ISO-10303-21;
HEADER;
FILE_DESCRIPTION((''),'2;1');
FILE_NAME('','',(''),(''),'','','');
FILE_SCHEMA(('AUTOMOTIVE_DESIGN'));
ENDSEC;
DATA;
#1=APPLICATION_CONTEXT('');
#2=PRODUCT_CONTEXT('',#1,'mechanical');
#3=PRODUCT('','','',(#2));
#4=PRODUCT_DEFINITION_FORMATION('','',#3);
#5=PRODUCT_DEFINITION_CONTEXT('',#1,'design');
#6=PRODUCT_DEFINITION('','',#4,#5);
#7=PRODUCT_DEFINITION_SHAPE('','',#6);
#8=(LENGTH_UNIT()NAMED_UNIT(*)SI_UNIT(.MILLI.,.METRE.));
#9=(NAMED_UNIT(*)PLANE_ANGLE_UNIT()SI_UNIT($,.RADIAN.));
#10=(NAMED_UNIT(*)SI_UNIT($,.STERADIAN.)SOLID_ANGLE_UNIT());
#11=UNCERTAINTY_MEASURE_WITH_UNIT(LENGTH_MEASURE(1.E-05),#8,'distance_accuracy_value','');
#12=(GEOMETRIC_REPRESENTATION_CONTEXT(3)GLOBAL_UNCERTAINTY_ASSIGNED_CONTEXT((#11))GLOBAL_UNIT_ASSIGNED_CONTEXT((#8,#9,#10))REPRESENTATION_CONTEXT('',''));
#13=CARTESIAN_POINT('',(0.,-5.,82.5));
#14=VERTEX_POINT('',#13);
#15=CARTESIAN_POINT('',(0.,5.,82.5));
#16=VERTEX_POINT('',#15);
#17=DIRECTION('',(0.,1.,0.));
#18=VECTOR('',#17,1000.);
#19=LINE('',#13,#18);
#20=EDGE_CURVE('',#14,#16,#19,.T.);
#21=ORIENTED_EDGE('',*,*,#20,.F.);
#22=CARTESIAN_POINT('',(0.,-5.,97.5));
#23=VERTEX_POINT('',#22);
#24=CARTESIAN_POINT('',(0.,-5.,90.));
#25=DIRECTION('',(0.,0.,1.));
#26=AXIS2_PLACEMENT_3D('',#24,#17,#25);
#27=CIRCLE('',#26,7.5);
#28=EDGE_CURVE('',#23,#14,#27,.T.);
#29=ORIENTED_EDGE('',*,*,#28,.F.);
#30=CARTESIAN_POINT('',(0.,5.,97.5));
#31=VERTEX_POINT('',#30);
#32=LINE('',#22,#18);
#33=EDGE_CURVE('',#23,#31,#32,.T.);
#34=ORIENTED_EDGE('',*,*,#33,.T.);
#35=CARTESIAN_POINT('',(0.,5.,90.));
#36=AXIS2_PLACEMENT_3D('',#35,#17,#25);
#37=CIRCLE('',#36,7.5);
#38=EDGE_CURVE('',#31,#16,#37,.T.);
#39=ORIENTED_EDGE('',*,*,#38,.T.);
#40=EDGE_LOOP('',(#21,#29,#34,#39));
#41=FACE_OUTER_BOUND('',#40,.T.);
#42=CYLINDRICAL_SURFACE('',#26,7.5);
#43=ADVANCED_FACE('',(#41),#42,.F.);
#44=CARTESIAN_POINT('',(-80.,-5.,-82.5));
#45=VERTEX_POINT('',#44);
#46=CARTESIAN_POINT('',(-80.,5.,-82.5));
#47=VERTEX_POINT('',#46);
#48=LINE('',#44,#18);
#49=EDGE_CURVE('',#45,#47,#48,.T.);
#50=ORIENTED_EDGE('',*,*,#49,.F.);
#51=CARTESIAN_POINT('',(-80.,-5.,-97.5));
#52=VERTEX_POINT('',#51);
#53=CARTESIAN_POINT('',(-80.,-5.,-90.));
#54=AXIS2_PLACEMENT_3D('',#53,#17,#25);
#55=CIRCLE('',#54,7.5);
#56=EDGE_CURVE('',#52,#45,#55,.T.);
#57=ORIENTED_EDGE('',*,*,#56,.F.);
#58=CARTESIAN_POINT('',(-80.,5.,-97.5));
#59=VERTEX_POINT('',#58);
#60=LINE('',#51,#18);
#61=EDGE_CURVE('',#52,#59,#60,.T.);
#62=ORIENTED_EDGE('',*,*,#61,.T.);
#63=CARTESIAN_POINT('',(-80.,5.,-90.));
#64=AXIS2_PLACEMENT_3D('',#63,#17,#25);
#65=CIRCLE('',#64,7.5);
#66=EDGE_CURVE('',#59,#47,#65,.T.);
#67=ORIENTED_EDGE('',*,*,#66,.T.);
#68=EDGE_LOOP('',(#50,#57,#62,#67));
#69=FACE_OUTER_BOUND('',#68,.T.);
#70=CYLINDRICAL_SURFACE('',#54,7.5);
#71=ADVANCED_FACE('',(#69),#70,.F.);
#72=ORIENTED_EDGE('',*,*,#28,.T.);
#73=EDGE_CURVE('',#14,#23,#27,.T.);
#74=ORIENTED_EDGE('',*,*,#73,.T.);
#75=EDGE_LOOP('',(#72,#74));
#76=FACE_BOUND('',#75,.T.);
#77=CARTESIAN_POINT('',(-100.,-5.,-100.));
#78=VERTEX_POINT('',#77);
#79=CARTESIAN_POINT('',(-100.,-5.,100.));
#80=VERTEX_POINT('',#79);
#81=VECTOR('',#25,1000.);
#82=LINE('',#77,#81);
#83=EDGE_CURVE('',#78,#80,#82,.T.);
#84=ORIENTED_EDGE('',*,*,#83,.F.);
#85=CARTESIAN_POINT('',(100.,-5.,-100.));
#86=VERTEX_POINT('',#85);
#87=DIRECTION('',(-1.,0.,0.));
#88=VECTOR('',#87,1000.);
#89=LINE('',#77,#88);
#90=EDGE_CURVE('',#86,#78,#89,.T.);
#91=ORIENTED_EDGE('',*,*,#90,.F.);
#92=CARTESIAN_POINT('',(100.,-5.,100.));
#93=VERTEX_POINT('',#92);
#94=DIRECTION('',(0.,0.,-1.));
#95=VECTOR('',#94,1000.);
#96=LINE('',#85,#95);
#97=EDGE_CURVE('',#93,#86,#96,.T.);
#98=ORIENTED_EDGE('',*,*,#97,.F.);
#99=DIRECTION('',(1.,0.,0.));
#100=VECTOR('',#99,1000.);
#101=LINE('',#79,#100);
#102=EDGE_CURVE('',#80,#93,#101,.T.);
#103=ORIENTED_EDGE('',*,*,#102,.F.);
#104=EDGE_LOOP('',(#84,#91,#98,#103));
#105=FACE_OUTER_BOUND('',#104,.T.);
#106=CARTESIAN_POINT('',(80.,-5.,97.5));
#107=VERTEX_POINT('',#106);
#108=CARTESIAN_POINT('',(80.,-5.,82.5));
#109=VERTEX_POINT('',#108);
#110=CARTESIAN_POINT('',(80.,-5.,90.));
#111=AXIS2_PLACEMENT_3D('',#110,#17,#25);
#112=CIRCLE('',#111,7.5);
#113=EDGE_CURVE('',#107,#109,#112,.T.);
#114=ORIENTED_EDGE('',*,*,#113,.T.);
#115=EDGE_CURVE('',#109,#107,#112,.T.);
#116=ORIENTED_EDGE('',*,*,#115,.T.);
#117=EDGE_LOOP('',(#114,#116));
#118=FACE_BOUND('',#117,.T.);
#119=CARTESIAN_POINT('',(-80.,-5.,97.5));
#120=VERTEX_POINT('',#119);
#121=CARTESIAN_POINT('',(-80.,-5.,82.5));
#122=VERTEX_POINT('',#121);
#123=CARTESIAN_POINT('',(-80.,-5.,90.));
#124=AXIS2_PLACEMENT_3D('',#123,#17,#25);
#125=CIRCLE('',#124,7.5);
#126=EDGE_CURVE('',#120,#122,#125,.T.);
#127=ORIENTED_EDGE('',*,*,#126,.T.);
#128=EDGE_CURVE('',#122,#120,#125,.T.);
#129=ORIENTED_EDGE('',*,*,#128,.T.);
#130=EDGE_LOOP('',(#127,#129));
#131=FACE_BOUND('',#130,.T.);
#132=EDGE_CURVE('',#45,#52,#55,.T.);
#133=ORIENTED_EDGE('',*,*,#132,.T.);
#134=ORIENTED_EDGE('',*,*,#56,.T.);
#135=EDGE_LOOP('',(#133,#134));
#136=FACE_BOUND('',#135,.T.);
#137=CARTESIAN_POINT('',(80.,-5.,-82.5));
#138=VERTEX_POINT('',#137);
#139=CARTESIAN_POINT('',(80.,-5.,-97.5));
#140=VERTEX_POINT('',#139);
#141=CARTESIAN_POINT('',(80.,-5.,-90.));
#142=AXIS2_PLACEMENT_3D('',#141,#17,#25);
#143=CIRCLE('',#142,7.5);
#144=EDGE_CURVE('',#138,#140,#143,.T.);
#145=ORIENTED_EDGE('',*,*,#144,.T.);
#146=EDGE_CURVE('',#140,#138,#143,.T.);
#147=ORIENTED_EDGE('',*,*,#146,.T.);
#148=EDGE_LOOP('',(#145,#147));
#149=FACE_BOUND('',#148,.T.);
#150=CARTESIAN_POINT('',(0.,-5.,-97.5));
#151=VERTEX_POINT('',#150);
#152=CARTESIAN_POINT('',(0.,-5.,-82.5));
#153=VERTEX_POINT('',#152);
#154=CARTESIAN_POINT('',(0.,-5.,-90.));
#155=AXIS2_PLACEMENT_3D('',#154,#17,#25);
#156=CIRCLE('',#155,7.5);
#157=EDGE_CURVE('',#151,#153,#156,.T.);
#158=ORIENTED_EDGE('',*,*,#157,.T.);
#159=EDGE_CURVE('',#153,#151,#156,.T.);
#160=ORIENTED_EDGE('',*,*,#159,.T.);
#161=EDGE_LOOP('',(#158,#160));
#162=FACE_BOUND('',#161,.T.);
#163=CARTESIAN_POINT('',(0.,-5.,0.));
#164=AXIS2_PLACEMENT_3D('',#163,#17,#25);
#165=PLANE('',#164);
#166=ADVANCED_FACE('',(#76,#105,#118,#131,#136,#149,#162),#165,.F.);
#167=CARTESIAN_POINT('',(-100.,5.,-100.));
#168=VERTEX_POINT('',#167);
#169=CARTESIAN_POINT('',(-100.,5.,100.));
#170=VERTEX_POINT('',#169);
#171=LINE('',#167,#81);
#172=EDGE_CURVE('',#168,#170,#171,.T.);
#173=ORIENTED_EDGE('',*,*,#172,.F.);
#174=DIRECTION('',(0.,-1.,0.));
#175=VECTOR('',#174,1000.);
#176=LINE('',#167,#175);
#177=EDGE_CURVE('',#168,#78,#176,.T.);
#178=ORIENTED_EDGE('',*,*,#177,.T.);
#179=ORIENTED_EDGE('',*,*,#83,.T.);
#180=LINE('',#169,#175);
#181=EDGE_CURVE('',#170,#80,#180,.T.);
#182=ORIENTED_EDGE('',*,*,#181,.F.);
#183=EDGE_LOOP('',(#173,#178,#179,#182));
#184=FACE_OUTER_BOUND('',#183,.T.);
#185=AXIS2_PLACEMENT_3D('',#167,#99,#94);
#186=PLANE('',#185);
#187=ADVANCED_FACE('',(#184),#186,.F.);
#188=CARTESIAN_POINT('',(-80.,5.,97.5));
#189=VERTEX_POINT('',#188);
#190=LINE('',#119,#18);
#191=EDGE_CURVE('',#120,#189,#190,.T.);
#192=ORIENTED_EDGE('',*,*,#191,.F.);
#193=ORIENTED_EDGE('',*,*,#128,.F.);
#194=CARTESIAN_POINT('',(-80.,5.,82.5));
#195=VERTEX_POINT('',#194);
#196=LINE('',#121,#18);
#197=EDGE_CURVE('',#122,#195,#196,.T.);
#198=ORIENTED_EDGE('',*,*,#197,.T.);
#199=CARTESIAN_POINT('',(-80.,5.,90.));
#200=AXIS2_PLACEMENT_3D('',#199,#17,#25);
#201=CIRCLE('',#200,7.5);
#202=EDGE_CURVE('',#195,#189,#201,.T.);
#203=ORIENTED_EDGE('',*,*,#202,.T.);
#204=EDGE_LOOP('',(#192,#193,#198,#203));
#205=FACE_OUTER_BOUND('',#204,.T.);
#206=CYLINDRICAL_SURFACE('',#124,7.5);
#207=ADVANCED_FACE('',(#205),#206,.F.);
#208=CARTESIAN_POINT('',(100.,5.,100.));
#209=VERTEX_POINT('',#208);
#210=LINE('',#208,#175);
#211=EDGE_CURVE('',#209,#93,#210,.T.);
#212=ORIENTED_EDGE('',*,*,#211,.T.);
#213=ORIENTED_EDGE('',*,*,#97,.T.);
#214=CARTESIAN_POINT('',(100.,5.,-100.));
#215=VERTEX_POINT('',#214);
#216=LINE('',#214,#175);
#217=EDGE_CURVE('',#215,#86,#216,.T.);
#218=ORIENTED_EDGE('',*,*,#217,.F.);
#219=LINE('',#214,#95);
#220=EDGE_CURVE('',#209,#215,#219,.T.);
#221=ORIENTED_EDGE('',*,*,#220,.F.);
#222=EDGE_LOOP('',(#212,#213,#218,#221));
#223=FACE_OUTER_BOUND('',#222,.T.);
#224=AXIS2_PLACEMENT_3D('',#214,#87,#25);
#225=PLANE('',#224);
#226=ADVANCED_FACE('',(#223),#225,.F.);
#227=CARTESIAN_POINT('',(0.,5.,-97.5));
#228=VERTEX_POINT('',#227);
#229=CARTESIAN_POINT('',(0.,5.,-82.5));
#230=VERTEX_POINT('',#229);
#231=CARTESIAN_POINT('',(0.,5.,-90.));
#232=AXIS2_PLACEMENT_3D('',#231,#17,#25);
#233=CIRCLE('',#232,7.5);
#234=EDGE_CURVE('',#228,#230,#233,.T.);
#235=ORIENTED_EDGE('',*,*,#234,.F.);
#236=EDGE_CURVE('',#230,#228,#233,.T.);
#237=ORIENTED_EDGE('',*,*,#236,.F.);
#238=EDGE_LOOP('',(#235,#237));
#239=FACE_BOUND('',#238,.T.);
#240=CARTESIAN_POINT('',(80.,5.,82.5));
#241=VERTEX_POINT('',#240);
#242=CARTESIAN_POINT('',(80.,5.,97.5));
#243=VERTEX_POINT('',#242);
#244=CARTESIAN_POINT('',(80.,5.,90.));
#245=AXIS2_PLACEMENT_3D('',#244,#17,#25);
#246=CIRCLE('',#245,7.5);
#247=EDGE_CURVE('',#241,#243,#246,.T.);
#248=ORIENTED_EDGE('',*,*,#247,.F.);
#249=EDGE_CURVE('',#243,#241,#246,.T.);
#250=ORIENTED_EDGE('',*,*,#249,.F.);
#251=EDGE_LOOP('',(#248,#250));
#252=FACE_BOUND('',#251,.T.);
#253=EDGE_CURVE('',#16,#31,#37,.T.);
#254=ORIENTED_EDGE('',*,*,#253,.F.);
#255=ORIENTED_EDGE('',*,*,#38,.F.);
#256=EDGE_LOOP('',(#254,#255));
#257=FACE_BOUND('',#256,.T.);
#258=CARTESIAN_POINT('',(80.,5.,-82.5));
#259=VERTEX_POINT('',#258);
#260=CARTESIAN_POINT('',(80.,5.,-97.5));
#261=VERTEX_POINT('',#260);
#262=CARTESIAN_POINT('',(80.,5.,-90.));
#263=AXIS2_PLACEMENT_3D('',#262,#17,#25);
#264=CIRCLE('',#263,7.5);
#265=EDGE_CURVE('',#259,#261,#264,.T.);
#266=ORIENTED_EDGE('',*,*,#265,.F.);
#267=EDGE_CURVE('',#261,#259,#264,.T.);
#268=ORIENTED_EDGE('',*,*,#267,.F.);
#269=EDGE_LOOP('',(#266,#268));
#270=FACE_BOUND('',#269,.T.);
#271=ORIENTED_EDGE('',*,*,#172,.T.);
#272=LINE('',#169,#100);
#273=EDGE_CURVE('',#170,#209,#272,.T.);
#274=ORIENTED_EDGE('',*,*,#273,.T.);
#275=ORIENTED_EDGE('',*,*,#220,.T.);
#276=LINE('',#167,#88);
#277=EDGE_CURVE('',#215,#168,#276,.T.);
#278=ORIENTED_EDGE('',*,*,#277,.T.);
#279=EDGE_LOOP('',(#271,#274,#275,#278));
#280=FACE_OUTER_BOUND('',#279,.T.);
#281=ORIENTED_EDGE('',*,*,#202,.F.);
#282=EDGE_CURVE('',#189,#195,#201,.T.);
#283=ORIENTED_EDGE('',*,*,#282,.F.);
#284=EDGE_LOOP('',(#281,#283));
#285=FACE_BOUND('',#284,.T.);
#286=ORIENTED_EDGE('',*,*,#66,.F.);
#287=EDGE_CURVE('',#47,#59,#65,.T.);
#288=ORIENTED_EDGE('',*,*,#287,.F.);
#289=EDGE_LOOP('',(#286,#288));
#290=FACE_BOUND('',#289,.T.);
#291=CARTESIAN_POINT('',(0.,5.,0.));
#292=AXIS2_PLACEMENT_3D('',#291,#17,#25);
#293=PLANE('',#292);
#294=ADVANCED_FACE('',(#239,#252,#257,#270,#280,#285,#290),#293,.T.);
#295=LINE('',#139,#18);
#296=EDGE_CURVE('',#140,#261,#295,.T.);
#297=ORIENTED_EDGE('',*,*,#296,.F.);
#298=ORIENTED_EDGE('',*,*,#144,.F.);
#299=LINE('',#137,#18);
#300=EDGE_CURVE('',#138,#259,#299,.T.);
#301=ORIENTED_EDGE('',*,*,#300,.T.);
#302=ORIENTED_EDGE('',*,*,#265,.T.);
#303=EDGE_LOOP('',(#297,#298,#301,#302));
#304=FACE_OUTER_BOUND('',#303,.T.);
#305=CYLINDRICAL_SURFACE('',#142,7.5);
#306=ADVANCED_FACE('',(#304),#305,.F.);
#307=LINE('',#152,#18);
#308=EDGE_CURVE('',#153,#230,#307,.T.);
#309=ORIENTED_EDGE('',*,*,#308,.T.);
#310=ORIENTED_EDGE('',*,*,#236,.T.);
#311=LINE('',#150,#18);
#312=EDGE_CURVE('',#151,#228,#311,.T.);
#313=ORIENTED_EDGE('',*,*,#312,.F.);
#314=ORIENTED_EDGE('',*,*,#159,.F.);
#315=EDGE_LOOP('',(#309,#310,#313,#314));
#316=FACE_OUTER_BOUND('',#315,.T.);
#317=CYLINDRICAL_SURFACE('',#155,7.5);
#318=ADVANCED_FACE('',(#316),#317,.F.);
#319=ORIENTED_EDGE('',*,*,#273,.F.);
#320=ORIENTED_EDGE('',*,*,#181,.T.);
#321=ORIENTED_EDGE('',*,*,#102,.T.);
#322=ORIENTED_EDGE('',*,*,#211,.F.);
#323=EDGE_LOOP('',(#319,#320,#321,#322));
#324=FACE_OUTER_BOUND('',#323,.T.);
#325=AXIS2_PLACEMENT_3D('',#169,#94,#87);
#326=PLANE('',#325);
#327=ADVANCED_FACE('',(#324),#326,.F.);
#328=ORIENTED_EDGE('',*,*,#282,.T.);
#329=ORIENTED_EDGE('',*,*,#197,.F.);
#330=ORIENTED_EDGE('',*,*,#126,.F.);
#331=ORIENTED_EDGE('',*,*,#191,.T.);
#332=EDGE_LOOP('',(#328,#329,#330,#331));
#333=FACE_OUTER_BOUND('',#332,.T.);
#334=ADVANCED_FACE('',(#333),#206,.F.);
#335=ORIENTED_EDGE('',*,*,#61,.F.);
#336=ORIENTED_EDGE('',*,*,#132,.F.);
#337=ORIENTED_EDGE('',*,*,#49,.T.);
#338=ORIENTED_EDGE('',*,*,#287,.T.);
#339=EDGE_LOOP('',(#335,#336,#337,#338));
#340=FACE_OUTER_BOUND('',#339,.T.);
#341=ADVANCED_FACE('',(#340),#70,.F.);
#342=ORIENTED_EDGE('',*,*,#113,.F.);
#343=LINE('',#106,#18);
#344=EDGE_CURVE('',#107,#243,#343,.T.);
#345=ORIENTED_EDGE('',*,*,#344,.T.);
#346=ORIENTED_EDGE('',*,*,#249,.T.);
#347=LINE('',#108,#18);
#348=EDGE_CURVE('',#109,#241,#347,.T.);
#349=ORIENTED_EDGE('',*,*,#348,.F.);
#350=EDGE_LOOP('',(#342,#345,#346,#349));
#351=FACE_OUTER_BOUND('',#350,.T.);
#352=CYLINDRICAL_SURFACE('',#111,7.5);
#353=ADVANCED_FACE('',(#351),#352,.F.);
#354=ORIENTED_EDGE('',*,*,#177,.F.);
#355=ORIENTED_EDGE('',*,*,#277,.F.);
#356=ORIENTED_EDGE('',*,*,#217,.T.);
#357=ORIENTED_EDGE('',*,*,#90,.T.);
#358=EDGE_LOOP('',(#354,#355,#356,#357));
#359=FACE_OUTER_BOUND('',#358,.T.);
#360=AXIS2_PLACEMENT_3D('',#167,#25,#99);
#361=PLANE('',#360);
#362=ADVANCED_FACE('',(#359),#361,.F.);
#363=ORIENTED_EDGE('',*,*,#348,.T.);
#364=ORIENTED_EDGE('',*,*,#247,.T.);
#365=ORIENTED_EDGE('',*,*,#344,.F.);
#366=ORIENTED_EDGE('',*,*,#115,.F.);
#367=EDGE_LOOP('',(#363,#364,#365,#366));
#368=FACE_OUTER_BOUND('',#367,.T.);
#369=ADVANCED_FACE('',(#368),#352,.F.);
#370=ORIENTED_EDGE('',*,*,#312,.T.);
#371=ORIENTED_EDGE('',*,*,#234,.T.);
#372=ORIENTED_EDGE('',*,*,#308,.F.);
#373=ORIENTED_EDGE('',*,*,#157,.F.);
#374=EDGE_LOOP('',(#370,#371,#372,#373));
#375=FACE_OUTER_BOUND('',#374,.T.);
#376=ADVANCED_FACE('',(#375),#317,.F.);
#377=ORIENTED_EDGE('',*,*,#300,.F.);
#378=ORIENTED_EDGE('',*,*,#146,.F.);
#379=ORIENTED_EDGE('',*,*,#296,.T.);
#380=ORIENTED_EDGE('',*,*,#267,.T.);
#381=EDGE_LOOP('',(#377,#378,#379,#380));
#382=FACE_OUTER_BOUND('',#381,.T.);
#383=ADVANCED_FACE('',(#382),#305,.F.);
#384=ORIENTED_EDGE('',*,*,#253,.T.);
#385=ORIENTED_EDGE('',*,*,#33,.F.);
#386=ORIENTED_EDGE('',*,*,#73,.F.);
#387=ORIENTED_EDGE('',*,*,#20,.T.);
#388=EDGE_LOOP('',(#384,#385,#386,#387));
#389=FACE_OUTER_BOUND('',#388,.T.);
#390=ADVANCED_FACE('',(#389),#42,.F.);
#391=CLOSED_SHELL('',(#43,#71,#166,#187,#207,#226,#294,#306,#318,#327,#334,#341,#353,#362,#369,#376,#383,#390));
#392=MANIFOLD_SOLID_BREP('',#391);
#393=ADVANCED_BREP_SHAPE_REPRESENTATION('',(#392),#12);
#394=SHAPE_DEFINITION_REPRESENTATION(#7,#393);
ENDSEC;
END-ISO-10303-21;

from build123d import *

# Parameters (mm, degrees)
SKETCH1_W            = 200
SKETCH1_H            = 200
BOSS_EXTRUDE1_DEPTH  = 5
SKETCH2_R            = 7.5
CUT_EXTRUDE1_DEPTH   = 10
LPATTERN1_COUNT      = 2
LPATTERN1_PITCH      = 180
LPATTERN1_COUNT_DIR2 = 3
LPATTERN1_PITCH_DIR2 = 80


with BuildPart() as part:
    # Sketch1 → Boss-Extrude1 (new, symmetric)
    with BuildSketch(Plane(origin=(0, 0, 0), x_dir=(1, 0, 0), z_dir=(0, 1, 0))):
        Rectangle(SKETCH1_W, SKETCH1_H)
    extrude(amount=BOSS_EXTRUDE1_DEPTH, both=True)

    # Sketch2 → Cut-Extrude1 (cut)
    with BuildSketch(Plane(origin=(0, 5, 0), x_dir=(1, 0, 0), z_dir=(0, 1, 0))):
        with Locations(Location((80, 90, 0), (0, 0, 270))):
            Circle(SKETCH2_R)
    cut_extrude1 = extrude(amount=-CUT_EXTRUDE1_DEPTH, mode=Mode.SUBTRACT)

    # LPattern1: Cut-Extrude1 2 × 3
    with Locations(*[(-j * LPATTERN1_PITCH_DIR2, 0, i * LPATTERN1_PITCH) for i in range(LPATTERN1_COUNT) for j in range(LPATTERN1_COUNT_DIR2) if (i, j) != (0, 0)]):
        add(cut_extrude1, mode=Mode.SUBTRACT)


solid = part.part
